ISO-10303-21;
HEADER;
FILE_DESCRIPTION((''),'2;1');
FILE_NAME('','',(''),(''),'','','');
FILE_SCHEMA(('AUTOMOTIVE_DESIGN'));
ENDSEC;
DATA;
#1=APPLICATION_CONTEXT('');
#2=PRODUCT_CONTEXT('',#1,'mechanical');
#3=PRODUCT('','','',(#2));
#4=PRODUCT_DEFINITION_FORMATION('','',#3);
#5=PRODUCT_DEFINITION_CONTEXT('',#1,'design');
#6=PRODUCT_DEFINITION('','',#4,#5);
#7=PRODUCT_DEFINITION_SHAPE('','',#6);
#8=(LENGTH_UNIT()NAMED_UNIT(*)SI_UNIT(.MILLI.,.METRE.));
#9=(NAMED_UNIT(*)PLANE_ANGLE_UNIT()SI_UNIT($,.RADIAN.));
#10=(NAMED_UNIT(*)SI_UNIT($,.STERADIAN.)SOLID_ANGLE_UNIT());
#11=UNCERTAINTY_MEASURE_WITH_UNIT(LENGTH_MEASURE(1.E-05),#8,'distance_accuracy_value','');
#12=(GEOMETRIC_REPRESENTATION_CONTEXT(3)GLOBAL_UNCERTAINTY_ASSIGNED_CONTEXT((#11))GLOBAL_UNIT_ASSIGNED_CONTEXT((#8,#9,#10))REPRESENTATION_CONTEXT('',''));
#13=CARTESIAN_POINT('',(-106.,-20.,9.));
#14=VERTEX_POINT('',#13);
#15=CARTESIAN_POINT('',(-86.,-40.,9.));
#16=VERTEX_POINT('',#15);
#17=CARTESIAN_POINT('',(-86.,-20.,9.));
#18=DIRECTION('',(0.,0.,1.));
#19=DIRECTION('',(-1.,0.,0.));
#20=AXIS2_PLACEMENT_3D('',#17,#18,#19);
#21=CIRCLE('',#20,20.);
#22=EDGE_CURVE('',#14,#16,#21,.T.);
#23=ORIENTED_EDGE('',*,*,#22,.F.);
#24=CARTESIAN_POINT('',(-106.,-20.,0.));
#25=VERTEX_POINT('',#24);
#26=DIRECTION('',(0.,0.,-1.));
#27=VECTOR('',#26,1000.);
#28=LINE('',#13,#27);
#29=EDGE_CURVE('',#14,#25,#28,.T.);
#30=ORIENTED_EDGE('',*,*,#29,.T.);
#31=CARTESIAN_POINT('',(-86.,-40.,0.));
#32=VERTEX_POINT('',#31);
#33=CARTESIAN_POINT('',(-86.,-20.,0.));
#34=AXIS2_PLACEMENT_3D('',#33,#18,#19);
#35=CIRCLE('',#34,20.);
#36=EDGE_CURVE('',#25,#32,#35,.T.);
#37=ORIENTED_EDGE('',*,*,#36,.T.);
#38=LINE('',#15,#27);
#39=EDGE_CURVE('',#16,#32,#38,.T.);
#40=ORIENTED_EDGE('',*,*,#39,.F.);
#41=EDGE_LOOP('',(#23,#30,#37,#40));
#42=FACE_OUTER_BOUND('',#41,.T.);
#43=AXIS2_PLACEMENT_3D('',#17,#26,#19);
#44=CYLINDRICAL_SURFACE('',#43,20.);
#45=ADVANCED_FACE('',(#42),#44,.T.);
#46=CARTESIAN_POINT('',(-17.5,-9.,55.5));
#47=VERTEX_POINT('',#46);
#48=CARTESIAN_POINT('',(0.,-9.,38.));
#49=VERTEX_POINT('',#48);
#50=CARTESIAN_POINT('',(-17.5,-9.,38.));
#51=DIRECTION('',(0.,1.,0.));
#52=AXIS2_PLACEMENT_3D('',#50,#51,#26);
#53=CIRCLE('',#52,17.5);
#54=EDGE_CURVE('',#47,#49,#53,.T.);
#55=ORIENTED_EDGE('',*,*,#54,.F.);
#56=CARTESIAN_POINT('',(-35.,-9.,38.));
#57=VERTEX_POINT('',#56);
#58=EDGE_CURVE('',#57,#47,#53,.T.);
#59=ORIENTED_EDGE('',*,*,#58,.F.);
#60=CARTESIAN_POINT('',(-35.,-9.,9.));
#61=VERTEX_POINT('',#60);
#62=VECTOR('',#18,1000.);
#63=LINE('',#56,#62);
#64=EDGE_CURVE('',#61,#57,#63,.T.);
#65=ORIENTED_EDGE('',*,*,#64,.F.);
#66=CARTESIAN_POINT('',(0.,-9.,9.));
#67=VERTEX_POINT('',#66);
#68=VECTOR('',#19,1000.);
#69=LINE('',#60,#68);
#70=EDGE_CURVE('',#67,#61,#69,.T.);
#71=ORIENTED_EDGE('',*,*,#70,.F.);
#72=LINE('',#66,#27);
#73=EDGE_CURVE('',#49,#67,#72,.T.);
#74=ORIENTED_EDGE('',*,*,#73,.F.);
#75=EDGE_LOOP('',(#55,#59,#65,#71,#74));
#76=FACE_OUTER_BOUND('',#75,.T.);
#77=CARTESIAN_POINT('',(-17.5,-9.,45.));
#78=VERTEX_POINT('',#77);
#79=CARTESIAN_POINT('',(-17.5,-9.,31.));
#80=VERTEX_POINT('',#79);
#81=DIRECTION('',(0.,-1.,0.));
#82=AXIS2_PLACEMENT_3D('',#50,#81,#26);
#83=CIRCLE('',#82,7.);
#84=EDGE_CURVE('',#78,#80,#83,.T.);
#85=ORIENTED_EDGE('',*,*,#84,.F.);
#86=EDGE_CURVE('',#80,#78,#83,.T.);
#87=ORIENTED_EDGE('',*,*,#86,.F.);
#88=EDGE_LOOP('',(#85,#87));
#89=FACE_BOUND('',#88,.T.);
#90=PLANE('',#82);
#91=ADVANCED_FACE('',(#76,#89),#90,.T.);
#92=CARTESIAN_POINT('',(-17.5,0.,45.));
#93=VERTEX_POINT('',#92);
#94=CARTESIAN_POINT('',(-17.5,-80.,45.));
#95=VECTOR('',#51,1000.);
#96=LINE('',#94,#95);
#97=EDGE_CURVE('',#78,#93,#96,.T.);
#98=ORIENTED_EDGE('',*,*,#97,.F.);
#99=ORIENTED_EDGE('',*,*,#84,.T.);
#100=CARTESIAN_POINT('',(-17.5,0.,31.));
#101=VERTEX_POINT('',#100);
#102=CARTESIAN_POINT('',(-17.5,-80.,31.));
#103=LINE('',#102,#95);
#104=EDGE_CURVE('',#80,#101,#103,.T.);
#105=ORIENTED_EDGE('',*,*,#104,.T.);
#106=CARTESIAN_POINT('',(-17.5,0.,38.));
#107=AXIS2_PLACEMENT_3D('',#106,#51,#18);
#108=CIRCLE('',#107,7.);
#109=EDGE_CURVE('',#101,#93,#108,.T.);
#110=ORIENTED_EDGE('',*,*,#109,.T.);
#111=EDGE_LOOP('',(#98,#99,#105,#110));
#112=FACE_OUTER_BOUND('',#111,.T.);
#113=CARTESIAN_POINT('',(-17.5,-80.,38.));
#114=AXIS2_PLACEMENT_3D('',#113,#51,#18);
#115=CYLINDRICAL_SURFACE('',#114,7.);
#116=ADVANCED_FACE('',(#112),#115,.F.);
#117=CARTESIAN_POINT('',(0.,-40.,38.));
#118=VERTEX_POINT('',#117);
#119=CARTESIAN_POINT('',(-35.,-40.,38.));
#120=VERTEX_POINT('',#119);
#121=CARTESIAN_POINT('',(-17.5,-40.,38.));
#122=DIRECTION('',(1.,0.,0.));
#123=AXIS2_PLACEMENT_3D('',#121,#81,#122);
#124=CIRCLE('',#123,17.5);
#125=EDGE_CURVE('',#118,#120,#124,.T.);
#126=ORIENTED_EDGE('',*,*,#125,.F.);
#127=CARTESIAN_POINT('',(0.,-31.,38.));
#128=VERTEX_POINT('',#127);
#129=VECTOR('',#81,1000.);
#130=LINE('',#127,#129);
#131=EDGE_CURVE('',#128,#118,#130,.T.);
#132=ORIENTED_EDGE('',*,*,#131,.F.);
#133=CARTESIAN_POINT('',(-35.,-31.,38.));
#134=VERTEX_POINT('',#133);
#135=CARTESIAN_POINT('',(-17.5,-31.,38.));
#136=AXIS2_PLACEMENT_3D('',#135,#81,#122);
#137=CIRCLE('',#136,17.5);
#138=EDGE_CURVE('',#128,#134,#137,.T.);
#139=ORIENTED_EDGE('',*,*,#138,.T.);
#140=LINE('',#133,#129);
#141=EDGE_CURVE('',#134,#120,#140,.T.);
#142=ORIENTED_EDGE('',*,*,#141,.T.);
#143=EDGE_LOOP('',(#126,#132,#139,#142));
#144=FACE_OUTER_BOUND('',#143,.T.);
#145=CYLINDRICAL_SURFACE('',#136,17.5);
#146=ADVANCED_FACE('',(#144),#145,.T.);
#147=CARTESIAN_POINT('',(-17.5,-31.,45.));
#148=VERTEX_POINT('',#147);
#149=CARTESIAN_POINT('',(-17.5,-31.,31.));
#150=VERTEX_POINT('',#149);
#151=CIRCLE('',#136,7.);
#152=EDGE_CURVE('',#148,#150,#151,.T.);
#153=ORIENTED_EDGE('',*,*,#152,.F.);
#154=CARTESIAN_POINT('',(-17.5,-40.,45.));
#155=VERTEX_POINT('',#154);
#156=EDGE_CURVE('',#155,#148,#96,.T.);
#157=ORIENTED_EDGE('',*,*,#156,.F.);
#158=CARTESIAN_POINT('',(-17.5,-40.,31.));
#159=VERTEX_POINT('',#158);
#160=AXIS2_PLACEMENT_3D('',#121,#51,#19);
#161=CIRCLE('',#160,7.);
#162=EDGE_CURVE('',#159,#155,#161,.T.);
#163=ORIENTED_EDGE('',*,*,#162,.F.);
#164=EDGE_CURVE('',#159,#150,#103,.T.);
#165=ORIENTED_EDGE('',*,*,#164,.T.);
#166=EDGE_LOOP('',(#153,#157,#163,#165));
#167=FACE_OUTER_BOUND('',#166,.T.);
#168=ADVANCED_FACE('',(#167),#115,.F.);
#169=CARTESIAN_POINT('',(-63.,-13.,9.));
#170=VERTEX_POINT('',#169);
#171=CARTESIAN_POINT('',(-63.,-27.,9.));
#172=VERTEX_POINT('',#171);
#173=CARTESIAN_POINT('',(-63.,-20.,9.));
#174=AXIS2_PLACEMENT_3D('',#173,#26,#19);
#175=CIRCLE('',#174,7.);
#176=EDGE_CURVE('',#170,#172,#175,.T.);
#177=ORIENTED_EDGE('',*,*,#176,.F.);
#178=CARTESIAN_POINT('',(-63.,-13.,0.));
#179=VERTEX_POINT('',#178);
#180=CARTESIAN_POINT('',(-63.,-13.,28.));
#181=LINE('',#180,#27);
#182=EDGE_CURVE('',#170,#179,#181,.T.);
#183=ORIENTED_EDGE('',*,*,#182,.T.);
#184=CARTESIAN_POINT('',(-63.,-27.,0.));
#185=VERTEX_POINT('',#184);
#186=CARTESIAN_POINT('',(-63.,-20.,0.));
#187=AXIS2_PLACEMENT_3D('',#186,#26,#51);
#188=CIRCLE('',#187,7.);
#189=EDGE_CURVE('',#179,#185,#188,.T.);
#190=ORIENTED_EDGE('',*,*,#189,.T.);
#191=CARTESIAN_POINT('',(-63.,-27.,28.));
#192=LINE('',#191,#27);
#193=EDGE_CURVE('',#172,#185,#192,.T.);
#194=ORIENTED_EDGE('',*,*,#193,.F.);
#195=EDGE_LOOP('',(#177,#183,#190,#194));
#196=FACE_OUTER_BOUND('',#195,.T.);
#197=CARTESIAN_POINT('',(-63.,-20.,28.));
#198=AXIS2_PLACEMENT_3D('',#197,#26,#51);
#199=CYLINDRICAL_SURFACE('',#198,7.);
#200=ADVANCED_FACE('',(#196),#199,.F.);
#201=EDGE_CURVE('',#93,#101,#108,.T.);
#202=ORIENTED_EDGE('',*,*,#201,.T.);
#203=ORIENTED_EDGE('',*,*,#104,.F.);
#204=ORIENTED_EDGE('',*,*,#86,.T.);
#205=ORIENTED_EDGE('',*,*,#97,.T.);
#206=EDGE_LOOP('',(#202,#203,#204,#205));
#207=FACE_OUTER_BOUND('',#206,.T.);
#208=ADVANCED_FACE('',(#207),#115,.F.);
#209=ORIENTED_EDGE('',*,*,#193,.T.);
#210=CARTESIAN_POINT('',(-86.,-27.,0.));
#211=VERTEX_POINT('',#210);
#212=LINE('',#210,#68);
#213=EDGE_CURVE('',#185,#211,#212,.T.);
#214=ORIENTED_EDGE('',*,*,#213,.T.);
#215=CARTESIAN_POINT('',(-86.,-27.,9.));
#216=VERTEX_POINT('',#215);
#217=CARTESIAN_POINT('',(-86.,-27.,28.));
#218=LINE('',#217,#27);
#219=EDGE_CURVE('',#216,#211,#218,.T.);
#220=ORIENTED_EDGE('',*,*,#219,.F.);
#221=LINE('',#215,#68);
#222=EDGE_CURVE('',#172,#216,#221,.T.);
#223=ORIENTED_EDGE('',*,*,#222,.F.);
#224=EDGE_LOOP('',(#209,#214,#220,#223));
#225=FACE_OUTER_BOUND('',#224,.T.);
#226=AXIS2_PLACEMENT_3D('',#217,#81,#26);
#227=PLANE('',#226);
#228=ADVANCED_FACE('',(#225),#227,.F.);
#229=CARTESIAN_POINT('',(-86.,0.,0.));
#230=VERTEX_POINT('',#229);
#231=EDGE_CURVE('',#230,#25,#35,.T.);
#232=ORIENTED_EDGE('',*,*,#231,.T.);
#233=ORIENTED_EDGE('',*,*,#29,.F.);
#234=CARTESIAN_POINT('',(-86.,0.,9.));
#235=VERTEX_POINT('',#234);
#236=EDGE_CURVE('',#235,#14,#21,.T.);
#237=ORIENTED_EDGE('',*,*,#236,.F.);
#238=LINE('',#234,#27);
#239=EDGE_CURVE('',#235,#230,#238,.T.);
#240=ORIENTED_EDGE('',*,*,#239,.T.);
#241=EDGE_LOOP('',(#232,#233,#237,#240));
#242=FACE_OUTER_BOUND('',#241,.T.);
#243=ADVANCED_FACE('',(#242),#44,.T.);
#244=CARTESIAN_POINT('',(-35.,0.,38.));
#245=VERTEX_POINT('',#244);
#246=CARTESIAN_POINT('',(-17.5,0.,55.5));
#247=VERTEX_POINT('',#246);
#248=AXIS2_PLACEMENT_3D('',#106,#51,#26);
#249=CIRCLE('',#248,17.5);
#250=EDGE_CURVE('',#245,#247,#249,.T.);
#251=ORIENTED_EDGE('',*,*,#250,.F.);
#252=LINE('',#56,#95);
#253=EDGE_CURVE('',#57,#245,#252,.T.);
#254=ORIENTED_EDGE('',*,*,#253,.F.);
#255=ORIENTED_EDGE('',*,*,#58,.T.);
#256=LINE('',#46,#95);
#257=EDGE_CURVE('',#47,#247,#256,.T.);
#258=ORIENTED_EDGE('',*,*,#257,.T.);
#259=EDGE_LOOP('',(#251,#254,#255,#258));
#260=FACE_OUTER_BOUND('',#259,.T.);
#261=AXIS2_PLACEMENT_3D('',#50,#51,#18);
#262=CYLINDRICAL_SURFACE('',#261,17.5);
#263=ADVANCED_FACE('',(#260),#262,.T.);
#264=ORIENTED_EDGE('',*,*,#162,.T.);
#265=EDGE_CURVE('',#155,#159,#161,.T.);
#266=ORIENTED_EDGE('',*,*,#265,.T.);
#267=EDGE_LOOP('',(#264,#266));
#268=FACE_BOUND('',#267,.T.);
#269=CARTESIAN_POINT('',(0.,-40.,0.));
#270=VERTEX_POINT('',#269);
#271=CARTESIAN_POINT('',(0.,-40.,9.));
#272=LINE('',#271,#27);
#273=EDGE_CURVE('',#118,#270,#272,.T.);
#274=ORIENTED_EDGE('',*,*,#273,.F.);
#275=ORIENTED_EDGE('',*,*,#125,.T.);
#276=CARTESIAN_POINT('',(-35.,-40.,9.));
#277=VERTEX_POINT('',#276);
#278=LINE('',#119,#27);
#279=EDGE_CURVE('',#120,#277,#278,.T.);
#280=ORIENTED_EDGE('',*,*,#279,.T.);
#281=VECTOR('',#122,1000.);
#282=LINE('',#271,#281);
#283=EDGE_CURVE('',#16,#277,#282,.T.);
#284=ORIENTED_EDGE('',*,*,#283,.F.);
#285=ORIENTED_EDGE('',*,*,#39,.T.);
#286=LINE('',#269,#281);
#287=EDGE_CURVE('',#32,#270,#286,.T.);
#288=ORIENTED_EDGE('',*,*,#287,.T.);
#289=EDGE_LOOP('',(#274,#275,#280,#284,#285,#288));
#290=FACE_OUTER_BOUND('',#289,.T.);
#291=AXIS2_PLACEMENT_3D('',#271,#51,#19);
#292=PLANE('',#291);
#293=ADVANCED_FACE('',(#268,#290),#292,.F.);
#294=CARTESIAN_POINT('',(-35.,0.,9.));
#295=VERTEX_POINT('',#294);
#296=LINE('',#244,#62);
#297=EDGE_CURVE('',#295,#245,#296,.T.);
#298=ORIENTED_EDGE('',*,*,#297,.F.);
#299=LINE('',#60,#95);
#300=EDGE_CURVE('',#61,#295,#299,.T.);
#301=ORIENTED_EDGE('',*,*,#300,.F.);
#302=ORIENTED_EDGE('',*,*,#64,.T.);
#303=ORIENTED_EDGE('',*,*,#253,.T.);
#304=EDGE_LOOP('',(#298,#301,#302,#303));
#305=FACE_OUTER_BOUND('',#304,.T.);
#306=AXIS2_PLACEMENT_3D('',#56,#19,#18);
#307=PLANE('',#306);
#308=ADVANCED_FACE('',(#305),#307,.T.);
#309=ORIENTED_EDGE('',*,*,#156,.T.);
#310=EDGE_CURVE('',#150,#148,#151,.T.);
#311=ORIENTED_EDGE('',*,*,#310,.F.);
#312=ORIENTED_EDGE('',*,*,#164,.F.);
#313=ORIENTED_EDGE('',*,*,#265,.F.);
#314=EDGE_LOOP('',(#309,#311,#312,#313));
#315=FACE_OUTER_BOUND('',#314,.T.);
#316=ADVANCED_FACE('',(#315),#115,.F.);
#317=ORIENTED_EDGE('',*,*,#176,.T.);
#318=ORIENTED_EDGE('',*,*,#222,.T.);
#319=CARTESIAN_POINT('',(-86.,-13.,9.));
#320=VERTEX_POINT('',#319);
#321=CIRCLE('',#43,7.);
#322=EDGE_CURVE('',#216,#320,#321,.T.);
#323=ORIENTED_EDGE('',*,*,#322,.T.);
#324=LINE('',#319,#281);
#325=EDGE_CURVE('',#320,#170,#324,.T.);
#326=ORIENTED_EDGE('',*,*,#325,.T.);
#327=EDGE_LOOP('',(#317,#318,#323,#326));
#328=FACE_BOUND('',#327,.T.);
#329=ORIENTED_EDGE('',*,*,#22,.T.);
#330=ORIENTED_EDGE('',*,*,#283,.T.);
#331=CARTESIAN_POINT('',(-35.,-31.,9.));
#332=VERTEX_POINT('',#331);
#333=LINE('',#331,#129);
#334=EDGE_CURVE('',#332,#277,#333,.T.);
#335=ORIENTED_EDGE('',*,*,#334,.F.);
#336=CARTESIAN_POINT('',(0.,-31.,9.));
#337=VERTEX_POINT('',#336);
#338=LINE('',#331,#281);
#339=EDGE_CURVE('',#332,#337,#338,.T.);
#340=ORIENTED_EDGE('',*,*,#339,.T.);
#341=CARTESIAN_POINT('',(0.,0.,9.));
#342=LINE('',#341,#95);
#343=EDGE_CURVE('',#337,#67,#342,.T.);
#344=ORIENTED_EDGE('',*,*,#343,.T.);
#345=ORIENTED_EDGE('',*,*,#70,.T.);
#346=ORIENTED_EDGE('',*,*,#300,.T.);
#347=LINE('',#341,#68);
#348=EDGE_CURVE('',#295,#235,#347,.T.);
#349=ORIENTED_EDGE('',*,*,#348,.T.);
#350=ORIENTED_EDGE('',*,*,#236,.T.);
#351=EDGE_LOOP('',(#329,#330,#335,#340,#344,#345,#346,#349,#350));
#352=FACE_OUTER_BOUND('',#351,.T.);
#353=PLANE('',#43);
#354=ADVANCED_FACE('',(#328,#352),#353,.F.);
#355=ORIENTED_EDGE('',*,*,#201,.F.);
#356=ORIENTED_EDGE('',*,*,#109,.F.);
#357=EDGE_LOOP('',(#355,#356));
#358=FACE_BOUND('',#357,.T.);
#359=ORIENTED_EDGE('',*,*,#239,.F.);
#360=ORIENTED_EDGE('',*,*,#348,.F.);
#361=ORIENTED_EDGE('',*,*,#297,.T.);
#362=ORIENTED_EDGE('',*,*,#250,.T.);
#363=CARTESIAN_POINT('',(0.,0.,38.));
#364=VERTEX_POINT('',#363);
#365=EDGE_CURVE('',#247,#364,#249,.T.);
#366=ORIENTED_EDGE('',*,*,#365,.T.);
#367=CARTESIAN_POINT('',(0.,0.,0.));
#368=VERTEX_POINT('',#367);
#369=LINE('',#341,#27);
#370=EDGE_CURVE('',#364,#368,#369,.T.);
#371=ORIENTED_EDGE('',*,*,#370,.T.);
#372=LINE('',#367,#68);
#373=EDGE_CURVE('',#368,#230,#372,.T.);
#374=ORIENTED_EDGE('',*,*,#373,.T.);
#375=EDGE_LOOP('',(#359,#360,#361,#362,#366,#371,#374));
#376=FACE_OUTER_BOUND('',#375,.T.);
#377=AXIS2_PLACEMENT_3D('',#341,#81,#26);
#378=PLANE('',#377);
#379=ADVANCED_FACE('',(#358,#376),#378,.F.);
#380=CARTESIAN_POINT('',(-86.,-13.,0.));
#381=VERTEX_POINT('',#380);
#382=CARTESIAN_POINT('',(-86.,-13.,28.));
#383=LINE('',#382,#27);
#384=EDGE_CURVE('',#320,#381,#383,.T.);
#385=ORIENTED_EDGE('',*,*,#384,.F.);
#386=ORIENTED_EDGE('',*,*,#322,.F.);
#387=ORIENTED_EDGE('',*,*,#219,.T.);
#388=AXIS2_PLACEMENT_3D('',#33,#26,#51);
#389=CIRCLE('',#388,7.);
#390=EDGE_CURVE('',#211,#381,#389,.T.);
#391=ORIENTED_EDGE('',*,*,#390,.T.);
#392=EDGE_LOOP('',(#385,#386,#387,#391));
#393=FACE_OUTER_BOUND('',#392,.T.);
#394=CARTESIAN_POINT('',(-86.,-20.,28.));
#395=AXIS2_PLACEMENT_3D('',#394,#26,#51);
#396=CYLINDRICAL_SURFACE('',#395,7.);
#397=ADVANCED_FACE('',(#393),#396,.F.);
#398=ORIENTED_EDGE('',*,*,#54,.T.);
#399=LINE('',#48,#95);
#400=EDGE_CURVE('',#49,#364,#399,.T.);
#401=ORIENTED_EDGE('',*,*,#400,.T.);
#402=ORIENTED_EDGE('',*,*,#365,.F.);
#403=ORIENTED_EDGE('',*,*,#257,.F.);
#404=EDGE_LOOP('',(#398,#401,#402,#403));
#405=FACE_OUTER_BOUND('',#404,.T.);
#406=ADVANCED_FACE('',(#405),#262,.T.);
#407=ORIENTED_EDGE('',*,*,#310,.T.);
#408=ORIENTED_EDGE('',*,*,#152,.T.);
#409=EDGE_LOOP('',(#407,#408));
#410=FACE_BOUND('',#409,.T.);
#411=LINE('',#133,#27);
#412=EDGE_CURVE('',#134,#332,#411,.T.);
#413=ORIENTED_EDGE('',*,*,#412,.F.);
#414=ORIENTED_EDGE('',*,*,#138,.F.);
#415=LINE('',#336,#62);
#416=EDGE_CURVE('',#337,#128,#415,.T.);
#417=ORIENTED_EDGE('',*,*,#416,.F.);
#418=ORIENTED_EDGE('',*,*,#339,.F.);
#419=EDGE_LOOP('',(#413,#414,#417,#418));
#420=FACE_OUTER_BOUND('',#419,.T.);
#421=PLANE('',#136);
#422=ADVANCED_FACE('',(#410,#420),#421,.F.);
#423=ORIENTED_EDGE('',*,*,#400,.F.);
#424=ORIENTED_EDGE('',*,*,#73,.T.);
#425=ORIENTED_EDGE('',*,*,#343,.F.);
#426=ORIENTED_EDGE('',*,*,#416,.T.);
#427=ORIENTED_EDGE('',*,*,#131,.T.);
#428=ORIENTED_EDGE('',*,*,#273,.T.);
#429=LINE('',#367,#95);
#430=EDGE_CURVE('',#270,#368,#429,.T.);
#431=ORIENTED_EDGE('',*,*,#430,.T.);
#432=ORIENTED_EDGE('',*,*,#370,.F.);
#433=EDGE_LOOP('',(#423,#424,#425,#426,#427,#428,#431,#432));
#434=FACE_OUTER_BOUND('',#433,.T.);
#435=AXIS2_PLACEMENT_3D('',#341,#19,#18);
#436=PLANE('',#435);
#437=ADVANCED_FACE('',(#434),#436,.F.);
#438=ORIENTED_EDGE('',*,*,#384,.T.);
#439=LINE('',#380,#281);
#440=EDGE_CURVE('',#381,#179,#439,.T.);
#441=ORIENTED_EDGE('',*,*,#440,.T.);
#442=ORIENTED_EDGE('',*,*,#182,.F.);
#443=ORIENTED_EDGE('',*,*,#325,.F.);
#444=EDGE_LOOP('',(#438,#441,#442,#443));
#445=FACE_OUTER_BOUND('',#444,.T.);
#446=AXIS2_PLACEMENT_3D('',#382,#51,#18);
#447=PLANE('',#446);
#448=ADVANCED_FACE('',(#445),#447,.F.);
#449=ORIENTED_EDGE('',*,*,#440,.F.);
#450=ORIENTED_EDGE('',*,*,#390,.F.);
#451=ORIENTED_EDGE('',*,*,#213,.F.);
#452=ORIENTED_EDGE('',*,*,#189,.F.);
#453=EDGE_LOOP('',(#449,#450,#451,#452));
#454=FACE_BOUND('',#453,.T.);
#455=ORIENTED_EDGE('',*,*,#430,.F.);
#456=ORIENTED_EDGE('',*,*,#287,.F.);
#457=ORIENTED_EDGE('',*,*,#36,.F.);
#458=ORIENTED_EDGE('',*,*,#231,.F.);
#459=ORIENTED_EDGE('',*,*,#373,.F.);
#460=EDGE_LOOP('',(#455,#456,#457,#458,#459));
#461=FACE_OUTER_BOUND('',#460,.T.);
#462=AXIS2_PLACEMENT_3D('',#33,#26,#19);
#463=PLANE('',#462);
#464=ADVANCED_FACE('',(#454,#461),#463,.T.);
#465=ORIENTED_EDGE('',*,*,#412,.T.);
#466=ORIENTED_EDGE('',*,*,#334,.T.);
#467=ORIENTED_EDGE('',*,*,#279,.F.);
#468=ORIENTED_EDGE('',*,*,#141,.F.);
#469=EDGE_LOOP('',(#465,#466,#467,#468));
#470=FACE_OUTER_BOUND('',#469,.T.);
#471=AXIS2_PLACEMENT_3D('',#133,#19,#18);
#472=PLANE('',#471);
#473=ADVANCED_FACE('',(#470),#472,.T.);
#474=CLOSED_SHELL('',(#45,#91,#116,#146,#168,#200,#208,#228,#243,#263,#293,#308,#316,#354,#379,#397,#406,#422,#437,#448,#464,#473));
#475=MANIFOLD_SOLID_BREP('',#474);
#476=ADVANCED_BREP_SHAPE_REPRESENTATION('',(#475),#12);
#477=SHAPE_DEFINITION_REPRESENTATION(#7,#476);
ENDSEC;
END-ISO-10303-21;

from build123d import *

# Parameters (mm, degrees)
BASE_PLATE_DEPTH   = 9
BASE_SLOT_DEPTH    = 28
CLEVIS_EAR_1_DEPTH = 9
CLEVIS_START       = -9
CLEVIS_EAR_2_DEPTH = 9
PIN_HOLE_SKETCH_R  = 7
PIN_HOLE_DEPTH     = 80


with BuildPart() as part:
    # Base Plate Sketch → Base Plate (new body)
    with BuildSketch(Plane(origin=(0, 0, 0), x_dir=(-1, 0, 0), z_dir=(0, 0, 1))):
        with BuildLine():
            Line((0, 0), (86, 0))
            ThreePointArc((86, 0), (106, 20), (86, 40))
            Line((86, 40), (0, 40))
            Line((0, 40), (0, 0))
        make_face()
    extrude(amount=BASE_PLATE_DEPTH)

    # Base Slot Sketch → Base Slot (cut)
    with BuildSketch(Plane(origin=(0, 0, 0), x_dir=(1, 0, 0), z_dir=(0, 0, -1))):
        with BuildLine():
            Line((-86, 27), (-63, 27))
            ThreePointArc((-63, 27), (-56, 20), (-63, 13))
            Line((-63, 13), (-86, 13))
            ThreePointArc((-86, 13), (-93, 20), (-86, 27))
        make_face()
    extrude(amount=-BASE_SLOT_DEPTH, mode=Mode.SUBTRACT)

    # Clevis Ear 1 Sketch → Clevis Ear 1 (add)
    with BuildSketch(Plane.XZ.offset(40)):
        with BuildLine():
            Line((0, 9), (0, 38))
            ThreePointArc((0, 38), (-17.5, 55.5), (-35, 38))
            Line((-35, 38), (-35, 9))
            Line((-35, 9), (0, 9))
        make_face()
    extrude(amount=-CLEVIS_EAR_1_DEPTH)

    # Clevis Ear 2 Sketch → Clevis Ear 2 (add)
    with BuildSketch(Plane(origin=(0, 0, 0), x_dir=(-1, 0, 0), z_dir=(0, 1, 0)).offset(CLEVIS_START)):
        with BuildLine():
            Line((0, 9), (0, 38))
            ThreePointArc((0, 38), (17.5, 55.5), (35, 38))
            Line((35, 38), (35, 9))
            Line((35, 9), (0, 9))
        make_face()
    extrude(amount=CLEVIS_EAR_2_DEPTH)

    # Pin Hole Sketch → Pin Hole (cut)
    with BuildSketch(Plane(origin=(0, 0, 0), x_dir=(-1, 0, 0), z_dir=(0, 1, 0))):
        with Locations(Location((17.5, 38, 0), (0, 0, 90))):
            Circle(PIN_HOLE_SKETCH_R)
    extrude(amount=-PIN_HOLE_DEPTH, mode=Mode.SUBTRACT)


solid = part.part
